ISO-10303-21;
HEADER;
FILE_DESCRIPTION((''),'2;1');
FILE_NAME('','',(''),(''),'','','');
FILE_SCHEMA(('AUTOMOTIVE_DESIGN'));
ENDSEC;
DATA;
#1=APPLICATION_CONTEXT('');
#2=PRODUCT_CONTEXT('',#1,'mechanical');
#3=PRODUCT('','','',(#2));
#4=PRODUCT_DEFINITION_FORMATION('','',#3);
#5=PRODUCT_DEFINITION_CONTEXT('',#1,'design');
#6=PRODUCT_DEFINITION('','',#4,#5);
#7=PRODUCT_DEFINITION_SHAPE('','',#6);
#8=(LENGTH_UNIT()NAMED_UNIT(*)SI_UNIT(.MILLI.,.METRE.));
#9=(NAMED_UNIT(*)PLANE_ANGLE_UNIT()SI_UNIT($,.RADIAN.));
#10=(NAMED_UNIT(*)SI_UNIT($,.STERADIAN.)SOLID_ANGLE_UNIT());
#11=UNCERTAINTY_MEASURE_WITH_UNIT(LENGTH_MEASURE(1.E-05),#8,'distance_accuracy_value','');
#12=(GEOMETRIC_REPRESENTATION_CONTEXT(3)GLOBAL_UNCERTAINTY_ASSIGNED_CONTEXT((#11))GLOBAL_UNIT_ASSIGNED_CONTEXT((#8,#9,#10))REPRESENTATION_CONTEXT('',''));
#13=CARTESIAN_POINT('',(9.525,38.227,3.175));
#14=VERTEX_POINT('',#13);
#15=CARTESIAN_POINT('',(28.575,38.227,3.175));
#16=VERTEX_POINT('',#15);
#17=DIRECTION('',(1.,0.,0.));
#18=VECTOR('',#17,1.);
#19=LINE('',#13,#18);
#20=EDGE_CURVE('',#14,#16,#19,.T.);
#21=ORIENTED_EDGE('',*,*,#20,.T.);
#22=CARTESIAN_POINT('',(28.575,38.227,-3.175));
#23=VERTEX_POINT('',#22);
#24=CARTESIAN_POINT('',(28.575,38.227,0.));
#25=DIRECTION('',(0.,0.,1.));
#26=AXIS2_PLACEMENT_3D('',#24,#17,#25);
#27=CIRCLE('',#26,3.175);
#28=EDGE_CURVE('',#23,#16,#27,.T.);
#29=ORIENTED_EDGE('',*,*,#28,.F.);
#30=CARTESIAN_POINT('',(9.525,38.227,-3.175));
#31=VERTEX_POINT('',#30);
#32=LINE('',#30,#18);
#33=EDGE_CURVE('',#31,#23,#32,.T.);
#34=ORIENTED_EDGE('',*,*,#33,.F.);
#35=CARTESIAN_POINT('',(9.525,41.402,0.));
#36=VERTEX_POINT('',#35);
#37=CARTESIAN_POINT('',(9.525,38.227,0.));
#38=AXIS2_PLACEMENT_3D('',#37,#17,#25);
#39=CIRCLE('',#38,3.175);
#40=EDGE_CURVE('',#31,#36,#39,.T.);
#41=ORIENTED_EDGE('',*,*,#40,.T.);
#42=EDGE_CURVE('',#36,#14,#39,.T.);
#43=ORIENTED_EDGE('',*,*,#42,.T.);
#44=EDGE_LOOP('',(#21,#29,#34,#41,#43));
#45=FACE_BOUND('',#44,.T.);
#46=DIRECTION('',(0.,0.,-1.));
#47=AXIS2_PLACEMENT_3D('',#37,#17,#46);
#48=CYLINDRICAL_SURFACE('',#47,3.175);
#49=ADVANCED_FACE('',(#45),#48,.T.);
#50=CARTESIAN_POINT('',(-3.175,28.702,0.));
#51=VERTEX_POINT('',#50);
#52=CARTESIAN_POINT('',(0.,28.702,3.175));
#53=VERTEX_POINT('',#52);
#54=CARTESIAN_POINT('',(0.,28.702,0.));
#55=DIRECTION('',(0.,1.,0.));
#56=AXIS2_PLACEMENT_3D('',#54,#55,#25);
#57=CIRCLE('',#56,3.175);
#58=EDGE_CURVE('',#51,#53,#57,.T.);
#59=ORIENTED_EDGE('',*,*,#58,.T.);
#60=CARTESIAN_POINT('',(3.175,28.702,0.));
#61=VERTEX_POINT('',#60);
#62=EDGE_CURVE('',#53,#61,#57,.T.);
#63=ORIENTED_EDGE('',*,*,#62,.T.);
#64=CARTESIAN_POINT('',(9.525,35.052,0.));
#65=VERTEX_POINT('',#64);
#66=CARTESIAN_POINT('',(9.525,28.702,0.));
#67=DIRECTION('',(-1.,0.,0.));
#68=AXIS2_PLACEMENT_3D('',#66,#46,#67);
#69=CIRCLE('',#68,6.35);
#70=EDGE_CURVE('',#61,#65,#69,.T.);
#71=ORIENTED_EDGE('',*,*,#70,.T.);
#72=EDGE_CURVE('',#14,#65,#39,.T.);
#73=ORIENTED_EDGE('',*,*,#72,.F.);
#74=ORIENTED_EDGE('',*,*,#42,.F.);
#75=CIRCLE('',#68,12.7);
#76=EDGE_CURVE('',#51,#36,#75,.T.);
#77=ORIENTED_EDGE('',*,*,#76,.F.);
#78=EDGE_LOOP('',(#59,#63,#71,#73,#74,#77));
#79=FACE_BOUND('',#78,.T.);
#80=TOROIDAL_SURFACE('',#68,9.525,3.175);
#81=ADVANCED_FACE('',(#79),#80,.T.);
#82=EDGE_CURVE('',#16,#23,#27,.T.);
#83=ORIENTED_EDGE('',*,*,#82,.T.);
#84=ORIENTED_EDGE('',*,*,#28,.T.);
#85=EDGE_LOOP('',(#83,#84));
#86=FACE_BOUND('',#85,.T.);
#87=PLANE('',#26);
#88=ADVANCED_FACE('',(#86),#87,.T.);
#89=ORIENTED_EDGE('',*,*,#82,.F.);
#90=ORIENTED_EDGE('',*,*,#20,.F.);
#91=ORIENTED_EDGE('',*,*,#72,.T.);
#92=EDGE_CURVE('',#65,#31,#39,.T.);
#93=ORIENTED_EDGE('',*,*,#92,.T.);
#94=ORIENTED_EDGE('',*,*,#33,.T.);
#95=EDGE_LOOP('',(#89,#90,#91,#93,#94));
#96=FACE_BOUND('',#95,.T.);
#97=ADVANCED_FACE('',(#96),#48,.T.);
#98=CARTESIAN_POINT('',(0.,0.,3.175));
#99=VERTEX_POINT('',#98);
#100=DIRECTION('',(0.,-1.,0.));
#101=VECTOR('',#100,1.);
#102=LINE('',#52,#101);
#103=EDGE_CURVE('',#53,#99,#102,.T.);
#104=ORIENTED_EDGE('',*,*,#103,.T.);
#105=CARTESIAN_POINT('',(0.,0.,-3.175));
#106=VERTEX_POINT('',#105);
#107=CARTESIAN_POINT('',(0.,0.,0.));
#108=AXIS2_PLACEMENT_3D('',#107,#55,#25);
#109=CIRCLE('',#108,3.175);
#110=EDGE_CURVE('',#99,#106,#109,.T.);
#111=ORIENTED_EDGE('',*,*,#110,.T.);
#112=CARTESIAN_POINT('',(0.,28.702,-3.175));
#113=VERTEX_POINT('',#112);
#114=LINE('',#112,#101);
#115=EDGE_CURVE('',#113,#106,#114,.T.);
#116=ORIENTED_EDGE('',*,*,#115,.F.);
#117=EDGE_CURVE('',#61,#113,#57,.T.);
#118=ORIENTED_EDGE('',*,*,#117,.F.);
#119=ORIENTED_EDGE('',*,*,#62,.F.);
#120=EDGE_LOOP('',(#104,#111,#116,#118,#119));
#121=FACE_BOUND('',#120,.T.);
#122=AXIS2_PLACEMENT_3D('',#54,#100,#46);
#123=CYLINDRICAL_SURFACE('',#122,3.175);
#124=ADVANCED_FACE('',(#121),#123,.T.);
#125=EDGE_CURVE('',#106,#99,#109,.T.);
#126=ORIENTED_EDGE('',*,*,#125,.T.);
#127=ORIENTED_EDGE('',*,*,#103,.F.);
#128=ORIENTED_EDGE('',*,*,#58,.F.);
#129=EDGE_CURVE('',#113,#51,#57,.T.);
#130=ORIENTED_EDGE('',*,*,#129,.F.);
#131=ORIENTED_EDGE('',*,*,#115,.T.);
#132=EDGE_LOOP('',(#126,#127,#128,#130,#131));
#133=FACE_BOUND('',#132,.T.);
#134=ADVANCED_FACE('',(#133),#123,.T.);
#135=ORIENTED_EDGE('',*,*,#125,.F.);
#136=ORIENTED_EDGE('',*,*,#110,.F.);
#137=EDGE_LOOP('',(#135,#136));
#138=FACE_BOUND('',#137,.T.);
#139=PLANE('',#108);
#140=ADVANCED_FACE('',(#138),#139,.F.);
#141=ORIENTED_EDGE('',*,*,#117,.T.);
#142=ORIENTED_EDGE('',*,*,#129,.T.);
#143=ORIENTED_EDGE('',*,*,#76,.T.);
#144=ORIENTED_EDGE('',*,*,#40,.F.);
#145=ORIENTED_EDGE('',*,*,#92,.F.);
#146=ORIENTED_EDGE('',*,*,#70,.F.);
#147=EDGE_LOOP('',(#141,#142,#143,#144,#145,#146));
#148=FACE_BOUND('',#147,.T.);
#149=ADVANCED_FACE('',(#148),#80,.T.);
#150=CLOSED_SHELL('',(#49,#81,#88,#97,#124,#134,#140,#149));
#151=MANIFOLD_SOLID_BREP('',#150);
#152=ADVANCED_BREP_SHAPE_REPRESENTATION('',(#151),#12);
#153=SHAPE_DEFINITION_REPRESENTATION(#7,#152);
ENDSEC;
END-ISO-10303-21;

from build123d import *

# Parameters (mm, degrees)
SKETCH2_R = 3.175


with BuildPart() as part:
    # Sweep1: sweep along a path in Sketch1
    with BuildLine(Plane.XY) as sweep1_path:
        Line((0, 0), (0, 28.702))
        ThreePointArc((0, 28.702), (2.789807909, 35.437192091), (9.525, 38.227))
        Line((9.525, 38.227), (28.575, 38.227))
    # Sketch2 → Sweep1 (sweep)
    with BuildSketch(Plane(origin=(0, 0, 0), x_dir=(1, 0, 0), z_dir=(0, 1, 0))):
        Circle(SKETCH2_R)
    sweep(path=sweep1_path.line)


solid = part.part
